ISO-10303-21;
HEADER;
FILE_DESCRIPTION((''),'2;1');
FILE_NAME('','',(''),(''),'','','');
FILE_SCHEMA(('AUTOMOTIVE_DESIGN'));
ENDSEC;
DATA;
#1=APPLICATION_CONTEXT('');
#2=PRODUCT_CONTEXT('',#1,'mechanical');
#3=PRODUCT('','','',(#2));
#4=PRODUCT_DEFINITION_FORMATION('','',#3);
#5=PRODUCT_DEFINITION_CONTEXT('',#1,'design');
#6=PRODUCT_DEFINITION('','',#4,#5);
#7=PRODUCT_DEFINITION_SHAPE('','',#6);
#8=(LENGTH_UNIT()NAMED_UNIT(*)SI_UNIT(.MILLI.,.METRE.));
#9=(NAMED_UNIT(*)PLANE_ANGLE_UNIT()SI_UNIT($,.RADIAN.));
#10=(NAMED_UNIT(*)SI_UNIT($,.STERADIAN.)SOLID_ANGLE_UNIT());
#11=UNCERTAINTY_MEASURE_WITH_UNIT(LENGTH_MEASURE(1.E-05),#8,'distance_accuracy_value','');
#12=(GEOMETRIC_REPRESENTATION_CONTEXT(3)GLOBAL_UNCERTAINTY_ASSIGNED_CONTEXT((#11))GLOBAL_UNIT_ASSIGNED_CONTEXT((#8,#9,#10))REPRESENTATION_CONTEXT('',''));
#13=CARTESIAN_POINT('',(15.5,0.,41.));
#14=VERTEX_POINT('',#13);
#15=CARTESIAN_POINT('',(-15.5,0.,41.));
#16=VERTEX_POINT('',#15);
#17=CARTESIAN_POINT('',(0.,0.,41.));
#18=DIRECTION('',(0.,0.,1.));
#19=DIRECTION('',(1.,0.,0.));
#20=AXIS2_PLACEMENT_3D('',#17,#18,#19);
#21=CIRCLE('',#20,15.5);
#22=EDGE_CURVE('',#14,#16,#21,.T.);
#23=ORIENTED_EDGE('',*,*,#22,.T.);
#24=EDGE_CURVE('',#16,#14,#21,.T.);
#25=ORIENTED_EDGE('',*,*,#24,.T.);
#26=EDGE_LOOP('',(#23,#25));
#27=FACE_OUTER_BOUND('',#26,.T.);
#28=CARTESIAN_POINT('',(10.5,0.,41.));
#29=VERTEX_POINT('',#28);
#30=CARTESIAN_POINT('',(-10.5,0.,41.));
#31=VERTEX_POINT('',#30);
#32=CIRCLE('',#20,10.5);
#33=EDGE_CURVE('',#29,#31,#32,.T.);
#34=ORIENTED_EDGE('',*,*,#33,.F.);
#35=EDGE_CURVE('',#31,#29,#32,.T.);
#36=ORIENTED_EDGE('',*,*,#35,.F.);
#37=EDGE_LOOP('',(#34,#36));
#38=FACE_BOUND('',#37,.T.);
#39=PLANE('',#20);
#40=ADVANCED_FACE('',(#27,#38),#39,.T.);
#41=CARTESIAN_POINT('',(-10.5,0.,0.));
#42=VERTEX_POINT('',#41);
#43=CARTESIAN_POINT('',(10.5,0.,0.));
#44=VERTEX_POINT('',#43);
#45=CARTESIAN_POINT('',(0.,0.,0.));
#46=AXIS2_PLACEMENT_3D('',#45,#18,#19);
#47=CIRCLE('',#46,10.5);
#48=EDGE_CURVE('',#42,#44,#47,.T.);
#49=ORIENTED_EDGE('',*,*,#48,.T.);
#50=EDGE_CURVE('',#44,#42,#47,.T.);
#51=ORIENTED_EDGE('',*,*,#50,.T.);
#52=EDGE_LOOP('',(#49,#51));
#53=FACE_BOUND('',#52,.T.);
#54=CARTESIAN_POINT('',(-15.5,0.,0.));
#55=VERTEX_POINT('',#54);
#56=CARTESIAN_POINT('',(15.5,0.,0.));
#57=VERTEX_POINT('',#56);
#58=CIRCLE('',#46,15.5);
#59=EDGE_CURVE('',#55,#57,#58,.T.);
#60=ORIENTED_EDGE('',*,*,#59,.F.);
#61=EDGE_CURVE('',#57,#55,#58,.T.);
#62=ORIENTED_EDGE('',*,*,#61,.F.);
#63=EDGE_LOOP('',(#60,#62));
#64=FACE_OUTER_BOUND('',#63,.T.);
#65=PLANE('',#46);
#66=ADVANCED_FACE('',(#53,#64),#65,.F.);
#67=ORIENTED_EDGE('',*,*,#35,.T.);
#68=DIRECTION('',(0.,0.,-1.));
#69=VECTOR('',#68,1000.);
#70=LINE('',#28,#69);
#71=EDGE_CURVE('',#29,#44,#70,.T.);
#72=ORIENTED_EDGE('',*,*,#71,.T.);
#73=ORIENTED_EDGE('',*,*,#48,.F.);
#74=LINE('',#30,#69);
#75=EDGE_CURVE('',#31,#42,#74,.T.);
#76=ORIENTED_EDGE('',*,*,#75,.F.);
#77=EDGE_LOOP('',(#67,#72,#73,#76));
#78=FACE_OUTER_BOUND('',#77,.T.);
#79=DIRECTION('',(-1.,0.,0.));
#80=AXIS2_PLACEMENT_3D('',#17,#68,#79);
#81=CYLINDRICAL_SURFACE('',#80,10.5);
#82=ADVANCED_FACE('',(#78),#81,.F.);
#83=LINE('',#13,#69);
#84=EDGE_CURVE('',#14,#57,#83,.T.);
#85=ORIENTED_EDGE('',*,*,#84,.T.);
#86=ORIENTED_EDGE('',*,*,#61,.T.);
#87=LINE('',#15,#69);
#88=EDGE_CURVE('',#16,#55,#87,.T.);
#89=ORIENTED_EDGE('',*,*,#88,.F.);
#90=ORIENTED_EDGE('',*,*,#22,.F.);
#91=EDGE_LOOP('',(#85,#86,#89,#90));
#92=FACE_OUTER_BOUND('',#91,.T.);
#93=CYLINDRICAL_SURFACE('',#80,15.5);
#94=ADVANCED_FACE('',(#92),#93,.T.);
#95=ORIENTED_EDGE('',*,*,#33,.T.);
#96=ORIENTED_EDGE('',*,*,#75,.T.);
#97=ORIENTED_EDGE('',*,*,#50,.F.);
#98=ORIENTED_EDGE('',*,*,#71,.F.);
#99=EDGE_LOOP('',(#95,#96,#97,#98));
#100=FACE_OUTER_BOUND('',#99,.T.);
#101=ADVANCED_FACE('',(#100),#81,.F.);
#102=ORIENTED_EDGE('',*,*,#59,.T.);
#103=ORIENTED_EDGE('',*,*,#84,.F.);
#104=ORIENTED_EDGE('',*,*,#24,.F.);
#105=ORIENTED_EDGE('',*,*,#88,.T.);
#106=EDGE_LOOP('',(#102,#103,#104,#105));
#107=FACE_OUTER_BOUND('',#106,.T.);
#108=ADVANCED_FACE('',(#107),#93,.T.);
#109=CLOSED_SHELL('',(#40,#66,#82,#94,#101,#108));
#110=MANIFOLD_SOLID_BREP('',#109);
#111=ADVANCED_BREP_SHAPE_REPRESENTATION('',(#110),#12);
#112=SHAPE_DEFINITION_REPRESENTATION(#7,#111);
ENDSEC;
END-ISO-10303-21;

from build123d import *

# Parameters (mm, degrees)
SKETCH1_R           = 15.5
SKETCH1_R_2         = 10.5
BOSS_EXTRUDE1_DEPTH = 41


with BuildPart() as part:
    # Sketch1 → Boss-Extrude1 (new body)
    with BuildSketch(Plane.XY):
        Circle(SKETCH1_R)
        Circle(SKETCH1_R_2, mode=Mode.SUBTRACT)
    extrude(amount=BOSS_EXTRUDE1_DEPTH)


solid = part.part
